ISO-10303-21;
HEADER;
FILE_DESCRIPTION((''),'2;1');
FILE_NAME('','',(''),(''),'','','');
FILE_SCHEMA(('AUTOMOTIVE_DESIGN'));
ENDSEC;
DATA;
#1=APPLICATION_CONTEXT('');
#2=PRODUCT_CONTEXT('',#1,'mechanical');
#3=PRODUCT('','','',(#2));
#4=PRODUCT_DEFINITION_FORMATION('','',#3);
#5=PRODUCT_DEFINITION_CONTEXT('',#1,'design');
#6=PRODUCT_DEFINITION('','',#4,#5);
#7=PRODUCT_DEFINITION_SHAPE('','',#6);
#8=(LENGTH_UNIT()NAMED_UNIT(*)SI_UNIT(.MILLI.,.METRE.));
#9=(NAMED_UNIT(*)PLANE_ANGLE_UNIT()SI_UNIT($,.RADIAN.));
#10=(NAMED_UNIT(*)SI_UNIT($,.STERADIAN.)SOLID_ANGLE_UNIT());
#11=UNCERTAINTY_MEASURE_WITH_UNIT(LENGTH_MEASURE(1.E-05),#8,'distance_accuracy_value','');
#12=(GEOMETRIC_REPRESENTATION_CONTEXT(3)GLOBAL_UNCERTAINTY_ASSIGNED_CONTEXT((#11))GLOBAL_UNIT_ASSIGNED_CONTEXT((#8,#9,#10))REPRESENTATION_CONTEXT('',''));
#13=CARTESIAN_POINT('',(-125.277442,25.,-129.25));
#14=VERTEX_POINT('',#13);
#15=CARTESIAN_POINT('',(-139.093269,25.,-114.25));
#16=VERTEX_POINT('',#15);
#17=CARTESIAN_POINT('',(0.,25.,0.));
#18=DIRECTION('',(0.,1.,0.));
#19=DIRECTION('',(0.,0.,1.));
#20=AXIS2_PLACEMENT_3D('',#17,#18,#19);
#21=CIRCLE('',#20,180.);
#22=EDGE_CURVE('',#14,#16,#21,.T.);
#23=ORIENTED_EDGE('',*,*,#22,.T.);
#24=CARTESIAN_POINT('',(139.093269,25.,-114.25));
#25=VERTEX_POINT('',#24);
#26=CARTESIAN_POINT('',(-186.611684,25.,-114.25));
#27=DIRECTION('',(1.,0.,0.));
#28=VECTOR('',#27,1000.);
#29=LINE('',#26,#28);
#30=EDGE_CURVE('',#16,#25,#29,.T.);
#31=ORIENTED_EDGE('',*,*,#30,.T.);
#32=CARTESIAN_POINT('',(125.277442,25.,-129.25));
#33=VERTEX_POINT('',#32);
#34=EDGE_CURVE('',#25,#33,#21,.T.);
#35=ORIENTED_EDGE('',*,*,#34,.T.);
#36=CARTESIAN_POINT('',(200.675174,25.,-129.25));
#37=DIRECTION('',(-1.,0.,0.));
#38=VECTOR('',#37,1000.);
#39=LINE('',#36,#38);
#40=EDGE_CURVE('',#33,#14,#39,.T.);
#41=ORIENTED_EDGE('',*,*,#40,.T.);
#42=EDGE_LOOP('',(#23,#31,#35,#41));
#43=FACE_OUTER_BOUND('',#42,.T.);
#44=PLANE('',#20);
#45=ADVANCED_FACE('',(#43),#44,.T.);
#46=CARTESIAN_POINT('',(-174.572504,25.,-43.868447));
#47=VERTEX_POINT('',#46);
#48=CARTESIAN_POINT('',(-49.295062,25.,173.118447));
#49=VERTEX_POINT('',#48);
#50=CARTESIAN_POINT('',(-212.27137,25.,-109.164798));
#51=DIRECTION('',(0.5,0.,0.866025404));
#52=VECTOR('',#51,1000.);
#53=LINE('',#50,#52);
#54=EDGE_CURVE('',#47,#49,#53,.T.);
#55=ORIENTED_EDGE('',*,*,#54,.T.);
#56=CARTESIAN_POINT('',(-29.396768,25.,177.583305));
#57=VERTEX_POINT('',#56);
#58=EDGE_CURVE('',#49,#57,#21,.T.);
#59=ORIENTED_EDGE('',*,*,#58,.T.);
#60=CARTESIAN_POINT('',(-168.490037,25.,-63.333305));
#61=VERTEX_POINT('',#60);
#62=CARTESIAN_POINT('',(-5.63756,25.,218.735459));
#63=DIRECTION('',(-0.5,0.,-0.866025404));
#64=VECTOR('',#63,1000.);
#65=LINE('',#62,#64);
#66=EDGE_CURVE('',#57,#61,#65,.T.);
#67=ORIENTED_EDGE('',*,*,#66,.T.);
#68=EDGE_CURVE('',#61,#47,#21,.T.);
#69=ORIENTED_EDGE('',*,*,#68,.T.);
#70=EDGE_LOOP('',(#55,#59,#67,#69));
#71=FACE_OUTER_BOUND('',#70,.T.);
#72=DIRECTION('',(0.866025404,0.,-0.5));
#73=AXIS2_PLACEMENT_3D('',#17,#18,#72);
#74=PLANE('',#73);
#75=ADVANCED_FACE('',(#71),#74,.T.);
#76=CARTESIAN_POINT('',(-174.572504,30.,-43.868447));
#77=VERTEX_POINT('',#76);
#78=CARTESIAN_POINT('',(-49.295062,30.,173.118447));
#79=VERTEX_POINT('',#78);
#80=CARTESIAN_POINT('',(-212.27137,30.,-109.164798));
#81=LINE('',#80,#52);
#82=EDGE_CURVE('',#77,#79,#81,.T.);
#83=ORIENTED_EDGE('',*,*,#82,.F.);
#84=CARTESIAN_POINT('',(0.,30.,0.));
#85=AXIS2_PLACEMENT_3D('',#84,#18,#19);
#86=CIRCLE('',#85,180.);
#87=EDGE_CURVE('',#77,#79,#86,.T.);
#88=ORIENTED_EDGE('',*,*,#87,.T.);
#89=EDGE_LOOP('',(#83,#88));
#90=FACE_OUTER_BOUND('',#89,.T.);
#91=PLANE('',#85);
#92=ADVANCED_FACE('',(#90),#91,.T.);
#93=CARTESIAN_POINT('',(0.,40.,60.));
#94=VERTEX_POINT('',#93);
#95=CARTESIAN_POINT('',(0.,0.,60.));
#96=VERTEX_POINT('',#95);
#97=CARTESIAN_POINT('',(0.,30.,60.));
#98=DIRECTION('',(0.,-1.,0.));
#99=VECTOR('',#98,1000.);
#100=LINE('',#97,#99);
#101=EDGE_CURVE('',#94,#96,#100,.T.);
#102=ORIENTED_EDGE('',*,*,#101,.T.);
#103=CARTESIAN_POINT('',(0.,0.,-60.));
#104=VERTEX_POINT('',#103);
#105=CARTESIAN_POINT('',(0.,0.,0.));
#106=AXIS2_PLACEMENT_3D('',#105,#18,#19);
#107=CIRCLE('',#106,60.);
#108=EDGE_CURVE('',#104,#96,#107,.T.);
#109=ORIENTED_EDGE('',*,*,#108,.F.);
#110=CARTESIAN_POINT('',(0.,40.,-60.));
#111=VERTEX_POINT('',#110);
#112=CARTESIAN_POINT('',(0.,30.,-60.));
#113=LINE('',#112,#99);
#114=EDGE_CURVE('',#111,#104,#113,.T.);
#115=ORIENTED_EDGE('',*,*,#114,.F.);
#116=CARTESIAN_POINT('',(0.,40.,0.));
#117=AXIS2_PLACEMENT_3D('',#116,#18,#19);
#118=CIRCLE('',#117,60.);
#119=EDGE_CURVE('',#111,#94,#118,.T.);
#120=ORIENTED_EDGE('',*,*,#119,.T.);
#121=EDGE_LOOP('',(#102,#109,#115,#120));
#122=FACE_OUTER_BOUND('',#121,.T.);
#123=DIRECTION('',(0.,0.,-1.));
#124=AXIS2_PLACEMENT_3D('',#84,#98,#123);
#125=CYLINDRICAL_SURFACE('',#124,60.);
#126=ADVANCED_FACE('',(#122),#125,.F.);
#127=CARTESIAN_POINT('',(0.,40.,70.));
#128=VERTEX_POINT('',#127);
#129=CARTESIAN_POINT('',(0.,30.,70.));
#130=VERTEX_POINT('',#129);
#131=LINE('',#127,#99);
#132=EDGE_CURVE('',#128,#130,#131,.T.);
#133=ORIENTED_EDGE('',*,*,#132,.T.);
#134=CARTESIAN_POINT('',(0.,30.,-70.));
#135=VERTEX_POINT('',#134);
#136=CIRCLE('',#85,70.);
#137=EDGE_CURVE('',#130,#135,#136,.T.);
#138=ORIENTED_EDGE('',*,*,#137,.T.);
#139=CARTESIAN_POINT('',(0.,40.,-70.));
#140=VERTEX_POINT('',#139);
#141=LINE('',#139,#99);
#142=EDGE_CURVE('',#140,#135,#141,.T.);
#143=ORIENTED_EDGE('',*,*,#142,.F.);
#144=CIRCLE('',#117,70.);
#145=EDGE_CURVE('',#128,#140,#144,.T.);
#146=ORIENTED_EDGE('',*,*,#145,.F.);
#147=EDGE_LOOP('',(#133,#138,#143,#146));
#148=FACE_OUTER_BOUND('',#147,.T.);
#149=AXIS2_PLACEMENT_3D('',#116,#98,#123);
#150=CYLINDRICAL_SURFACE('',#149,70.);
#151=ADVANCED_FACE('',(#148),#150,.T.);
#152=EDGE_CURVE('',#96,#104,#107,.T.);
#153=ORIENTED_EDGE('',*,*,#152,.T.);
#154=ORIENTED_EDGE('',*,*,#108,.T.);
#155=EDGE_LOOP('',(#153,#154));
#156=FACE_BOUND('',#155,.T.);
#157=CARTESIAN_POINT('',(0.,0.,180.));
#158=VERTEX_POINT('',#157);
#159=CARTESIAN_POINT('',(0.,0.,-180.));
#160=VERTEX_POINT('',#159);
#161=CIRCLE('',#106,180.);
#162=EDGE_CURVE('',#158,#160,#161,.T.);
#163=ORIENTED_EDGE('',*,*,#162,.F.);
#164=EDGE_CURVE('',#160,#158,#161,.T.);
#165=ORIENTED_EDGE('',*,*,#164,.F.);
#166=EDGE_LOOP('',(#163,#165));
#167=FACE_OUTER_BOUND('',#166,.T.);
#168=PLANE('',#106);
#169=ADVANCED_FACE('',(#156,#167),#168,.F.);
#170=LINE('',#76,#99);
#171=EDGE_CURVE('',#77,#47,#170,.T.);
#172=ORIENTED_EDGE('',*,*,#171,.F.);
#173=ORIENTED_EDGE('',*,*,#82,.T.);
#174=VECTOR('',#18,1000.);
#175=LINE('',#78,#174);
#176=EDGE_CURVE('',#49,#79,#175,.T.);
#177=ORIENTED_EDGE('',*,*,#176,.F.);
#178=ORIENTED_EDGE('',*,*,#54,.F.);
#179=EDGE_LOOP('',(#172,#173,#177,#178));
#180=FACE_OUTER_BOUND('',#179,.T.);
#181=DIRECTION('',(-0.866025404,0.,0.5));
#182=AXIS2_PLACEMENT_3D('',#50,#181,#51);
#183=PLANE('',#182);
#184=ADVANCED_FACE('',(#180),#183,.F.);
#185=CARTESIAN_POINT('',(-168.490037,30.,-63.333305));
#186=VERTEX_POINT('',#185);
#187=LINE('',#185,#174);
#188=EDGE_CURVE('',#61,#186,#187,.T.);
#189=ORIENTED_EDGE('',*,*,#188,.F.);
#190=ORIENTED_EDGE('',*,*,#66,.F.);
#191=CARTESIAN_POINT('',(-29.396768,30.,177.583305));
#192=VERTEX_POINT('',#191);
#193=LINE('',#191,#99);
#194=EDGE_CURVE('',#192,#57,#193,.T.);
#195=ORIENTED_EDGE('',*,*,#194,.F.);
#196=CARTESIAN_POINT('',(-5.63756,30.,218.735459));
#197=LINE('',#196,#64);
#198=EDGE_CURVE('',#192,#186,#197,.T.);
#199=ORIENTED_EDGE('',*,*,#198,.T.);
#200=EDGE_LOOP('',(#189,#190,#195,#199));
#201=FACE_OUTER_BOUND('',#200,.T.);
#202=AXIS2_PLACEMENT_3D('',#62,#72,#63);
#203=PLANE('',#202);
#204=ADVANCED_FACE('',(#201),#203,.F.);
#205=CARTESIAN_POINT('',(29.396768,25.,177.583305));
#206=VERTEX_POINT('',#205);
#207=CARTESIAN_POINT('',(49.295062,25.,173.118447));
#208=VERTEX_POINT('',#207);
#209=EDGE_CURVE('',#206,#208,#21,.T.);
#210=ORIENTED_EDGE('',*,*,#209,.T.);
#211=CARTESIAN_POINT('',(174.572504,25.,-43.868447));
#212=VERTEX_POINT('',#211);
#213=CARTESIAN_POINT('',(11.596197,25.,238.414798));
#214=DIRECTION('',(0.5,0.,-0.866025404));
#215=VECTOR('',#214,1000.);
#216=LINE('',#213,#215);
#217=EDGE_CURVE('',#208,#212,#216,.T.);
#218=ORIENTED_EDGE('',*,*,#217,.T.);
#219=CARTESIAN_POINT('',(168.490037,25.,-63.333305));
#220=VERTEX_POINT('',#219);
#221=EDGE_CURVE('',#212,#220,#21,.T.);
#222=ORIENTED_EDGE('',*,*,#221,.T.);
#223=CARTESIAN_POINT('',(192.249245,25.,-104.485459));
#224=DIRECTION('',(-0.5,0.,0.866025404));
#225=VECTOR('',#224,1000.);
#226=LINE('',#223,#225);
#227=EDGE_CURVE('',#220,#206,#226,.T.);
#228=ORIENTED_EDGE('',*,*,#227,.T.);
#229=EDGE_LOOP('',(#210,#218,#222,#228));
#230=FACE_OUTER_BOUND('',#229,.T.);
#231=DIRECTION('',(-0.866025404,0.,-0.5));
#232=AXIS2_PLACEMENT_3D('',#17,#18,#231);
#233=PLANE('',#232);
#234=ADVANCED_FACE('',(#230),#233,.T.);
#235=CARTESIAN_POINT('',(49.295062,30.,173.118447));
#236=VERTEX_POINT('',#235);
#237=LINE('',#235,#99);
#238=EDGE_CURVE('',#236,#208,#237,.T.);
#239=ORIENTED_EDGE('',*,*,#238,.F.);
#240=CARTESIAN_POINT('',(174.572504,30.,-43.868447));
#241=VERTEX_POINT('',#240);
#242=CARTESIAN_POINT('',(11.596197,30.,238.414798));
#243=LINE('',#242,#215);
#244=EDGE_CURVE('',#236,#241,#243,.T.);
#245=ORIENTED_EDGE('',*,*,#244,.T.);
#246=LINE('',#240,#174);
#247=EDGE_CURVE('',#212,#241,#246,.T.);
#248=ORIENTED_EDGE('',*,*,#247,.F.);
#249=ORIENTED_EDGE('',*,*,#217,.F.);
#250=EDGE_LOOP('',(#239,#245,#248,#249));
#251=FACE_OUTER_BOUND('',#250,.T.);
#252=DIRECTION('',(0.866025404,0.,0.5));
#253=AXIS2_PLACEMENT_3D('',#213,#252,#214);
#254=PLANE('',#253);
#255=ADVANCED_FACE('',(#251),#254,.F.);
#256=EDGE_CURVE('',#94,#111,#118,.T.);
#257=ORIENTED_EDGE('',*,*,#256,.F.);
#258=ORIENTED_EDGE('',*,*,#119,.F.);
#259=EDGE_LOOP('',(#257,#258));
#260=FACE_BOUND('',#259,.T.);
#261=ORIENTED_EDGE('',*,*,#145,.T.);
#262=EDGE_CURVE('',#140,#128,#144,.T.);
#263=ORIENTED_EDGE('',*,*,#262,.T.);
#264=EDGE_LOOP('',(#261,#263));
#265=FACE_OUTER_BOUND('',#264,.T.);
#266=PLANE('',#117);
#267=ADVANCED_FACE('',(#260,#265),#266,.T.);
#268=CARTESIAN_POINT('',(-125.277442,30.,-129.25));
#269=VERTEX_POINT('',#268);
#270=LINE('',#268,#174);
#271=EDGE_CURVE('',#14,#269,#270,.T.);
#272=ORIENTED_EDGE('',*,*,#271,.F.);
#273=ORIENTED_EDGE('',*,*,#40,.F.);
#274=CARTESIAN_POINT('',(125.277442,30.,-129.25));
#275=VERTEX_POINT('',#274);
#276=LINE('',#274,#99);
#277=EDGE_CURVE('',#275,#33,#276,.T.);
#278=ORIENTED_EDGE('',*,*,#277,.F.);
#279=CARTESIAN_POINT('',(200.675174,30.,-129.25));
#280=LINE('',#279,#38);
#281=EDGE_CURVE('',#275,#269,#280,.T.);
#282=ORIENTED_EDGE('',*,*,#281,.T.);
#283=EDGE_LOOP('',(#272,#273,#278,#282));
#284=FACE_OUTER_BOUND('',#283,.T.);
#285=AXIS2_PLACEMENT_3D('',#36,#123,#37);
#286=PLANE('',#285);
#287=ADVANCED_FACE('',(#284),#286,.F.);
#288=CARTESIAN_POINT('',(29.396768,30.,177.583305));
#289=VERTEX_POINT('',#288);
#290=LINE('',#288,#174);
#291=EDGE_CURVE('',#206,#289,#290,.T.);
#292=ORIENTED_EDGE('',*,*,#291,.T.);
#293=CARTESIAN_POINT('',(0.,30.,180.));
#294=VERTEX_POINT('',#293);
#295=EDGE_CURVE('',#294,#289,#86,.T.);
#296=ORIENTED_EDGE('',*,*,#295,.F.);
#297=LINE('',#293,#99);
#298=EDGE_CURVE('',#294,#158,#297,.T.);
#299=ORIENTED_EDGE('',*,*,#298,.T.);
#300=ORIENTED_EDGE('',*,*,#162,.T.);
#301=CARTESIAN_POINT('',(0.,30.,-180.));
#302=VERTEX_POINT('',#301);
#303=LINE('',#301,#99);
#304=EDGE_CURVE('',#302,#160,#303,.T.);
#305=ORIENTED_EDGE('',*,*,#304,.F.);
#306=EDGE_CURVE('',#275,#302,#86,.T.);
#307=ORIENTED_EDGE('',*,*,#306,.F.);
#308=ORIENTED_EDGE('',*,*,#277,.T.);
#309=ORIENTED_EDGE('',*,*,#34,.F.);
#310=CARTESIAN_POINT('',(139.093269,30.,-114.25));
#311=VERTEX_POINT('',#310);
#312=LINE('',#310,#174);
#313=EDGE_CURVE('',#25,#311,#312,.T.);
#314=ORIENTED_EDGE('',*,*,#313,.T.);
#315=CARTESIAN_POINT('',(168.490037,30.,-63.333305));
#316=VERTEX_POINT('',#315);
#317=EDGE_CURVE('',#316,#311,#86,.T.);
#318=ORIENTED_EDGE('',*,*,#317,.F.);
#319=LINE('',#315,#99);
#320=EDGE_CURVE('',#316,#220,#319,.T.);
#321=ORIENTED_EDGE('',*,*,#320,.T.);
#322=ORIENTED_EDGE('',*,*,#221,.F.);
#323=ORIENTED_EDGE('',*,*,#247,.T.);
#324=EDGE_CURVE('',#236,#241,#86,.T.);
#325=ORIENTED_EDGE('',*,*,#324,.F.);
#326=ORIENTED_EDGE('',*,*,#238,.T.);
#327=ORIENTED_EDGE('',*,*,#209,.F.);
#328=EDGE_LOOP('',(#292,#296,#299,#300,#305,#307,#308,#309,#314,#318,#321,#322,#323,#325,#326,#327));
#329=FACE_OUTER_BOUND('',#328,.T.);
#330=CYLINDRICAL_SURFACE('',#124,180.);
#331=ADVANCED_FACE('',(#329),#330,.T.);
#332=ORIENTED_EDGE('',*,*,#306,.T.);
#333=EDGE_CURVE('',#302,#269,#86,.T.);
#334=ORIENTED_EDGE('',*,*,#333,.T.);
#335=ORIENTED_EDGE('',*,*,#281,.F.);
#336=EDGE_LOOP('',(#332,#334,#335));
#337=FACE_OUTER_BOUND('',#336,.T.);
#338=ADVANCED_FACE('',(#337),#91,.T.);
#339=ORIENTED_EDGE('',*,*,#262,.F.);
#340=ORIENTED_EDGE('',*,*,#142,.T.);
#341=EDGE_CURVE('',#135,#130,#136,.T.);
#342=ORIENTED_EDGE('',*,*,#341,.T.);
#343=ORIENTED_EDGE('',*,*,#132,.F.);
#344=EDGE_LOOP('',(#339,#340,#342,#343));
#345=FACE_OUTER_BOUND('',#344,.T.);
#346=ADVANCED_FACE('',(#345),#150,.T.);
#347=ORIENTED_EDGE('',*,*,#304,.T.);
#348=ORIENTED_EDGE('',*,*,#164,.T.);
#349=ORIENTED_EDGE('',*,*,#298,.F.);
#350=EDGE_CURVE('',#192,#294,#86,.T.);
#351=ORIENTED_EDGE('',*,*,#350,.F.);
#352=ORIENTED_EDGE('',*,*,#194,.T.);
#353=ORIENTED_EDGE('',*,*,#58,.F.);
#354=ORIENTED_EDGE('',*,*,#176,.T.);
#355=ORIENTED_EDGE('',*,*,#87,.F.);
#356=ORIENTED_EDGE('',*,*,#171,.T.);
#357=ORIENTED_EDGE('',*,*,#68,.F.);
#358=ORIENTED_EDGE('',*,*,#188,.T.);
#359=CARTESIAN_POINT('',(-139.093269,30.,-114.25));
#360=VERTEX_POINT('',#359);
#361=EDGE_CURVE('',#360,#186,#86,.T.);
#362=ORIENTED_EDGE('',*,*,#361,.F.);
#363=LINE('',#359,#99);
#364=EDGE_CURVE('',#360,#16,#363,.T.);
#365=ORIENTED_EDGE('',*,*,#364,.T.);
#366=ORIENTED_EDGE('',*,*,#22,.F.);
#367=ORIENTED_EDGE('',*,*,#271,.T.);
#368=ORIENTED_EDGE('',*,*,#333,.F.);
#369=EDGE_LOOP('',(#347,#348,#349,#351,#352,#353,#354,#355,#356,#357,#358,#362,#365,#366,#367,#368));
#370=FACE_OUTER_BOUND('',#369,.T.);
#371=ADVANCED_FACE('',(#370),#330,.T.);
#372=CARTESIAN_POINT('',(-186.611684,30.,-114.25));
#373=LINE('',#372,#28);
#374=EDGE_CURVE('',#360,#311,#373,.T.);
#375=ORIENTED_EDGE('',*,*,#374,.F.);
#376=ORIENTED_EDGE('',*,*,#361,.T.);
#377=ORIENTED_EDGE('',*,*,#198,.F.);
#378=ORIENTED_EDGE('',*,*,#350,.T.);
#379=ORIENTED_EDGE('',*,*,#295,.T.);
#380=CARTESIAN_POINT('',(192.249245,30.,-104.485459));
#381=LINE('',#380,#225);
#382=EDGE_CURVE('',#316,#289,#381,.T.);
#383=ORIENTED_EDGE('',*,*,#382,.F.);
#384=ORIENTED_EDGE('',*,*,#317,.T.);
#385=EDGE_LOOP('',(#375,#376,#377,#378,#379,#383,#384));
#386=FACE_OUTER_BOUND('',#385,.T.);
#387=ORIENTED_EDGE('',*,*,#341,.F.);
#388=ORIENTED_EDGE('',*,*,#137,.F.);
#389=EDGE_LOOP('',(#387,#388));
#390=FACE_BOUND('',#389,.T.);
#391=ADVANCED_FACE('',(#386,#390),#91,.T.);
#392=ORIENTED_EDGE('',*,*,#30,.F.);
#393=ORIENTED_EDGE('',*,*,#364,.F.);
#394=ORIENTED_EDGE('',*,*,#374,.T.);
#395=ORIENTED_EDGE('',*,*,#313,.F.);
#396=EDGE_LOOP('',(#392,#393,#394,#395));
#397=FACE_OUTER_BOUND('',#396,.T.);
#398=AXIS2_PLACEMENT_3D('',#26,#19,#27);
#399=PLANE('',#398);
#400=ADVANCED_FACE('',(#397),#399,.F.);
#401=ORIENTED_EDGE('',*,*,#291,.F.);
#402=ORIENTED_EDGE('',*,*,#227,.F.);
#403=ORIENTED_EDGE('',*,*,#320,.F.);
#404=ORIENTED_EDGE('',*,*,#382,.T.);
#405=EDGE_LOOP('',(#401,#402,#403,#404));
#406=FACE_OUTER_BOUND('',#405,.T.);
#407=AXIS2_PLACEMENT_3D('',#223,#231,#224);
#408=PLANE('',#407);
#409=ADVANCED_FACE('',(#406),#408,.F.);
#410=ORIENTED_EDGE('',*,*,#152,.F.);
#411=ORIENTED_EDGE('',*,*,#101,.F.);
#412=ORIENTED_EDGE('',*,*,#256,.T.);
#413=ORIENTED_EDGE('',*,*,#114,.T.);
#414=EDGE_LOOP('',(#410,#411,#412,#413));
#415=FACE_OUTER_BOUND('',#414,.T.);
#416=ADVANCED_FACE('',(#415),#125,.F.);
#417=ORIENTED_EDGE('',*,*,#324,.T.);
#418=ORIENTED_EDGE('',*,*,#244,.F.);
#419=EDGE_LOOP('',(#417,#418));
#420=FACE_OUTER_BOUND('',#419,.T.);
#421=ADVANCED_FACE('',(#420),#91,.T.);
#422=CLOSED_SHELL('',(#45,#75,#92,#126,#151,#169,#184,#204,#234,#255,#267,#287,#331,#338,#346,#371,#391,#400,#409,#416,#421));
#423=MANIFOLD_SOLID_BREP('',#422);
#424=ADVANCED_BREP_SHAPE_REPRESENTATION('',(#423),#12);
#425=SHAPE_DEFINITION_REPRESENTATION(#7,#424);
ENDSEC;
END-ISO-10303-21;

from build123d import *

# Parameters (mm, degrees)
SKETCH1_R           = 180
SKETCH1_R_2         = 60
BOSS_EXTRUDE1_DEPTH = 30
SKETCH2_R           = 70
SKETCH2_R_2         = 60
BOSS_EXTRUDE2_DEPTH = 10
SKETCH4_W           = 387.286858061
SKETCH4_H           = 15
CUT_EXTRUDE2_DEPTH  = 5
CIRPATTERN1_COUNT   = 3


with BuildPart() as part:
    # Sketch1 → Boss-Extrude1 (new body)
    with BuildSketch(Plane(origin=(0, 0, 0), x_dir=(1, 0, 0), z_dir=(0, 1, 0))):
        with Locations(Location((0, 0, 0), (0, 0, 270))):
            Circle(SKETCH1_R)
        with Locations(Location((0, 0, 0), (0, 0, 270))):
            Circle(SKETCH1_R_2, mode=Mode.SUBTRACT)
    extrude(amount=BOSS_EXTRUDE1_DEPTH)

    # Sketch2 → Boss-Extrude2 (add)
    with BuildSketch(Plane(origin=(0, 30, 0), x_dir=(1, 0, 0), z_dir=(0, 1, 0))):
        with Locations(Location((0, 0, 0), (0, 0, 270))):
            Circle(SKETCH2_R)
        with Locations(Location((0, 0, 0), (0, 0, 270))):
            Circle(SKETCH2_R_2, mode=Mode.SUBTRACT)
    extrude(amount=BOSS_EXTRUDE2_DEPTH)

    # Sketch4 → Cut-Extrude2 (cut)
    with BuildSketch(Plane(origin=(0, 30, 0), x_dir=(1, 0, 0), z_dir=(0, 1, 0))):
        with Locations((7.031744629, 121.75)):
            Rectangle(SKETCH4_W, SKETCH4_H)
    cut_extrude2 = extrude(amount=-CUT_EXTRUDE2_DEPTH, mode=Mode.SUBTRACT)

    # CirPattern1: Cut-Extrude2 ×3 about axis
    cirpattern1_axis = Axis((0, 0, 0), (0, 1, 0))
    for i in range(1, CIRPATTERN1_COUNT):
        add(cut_extrude2.rotate(cirpattern1_axis, i * 360 / CIRPATTERN1_COUNT), mode=Mode.SUBTRACT)


solid = part.part
